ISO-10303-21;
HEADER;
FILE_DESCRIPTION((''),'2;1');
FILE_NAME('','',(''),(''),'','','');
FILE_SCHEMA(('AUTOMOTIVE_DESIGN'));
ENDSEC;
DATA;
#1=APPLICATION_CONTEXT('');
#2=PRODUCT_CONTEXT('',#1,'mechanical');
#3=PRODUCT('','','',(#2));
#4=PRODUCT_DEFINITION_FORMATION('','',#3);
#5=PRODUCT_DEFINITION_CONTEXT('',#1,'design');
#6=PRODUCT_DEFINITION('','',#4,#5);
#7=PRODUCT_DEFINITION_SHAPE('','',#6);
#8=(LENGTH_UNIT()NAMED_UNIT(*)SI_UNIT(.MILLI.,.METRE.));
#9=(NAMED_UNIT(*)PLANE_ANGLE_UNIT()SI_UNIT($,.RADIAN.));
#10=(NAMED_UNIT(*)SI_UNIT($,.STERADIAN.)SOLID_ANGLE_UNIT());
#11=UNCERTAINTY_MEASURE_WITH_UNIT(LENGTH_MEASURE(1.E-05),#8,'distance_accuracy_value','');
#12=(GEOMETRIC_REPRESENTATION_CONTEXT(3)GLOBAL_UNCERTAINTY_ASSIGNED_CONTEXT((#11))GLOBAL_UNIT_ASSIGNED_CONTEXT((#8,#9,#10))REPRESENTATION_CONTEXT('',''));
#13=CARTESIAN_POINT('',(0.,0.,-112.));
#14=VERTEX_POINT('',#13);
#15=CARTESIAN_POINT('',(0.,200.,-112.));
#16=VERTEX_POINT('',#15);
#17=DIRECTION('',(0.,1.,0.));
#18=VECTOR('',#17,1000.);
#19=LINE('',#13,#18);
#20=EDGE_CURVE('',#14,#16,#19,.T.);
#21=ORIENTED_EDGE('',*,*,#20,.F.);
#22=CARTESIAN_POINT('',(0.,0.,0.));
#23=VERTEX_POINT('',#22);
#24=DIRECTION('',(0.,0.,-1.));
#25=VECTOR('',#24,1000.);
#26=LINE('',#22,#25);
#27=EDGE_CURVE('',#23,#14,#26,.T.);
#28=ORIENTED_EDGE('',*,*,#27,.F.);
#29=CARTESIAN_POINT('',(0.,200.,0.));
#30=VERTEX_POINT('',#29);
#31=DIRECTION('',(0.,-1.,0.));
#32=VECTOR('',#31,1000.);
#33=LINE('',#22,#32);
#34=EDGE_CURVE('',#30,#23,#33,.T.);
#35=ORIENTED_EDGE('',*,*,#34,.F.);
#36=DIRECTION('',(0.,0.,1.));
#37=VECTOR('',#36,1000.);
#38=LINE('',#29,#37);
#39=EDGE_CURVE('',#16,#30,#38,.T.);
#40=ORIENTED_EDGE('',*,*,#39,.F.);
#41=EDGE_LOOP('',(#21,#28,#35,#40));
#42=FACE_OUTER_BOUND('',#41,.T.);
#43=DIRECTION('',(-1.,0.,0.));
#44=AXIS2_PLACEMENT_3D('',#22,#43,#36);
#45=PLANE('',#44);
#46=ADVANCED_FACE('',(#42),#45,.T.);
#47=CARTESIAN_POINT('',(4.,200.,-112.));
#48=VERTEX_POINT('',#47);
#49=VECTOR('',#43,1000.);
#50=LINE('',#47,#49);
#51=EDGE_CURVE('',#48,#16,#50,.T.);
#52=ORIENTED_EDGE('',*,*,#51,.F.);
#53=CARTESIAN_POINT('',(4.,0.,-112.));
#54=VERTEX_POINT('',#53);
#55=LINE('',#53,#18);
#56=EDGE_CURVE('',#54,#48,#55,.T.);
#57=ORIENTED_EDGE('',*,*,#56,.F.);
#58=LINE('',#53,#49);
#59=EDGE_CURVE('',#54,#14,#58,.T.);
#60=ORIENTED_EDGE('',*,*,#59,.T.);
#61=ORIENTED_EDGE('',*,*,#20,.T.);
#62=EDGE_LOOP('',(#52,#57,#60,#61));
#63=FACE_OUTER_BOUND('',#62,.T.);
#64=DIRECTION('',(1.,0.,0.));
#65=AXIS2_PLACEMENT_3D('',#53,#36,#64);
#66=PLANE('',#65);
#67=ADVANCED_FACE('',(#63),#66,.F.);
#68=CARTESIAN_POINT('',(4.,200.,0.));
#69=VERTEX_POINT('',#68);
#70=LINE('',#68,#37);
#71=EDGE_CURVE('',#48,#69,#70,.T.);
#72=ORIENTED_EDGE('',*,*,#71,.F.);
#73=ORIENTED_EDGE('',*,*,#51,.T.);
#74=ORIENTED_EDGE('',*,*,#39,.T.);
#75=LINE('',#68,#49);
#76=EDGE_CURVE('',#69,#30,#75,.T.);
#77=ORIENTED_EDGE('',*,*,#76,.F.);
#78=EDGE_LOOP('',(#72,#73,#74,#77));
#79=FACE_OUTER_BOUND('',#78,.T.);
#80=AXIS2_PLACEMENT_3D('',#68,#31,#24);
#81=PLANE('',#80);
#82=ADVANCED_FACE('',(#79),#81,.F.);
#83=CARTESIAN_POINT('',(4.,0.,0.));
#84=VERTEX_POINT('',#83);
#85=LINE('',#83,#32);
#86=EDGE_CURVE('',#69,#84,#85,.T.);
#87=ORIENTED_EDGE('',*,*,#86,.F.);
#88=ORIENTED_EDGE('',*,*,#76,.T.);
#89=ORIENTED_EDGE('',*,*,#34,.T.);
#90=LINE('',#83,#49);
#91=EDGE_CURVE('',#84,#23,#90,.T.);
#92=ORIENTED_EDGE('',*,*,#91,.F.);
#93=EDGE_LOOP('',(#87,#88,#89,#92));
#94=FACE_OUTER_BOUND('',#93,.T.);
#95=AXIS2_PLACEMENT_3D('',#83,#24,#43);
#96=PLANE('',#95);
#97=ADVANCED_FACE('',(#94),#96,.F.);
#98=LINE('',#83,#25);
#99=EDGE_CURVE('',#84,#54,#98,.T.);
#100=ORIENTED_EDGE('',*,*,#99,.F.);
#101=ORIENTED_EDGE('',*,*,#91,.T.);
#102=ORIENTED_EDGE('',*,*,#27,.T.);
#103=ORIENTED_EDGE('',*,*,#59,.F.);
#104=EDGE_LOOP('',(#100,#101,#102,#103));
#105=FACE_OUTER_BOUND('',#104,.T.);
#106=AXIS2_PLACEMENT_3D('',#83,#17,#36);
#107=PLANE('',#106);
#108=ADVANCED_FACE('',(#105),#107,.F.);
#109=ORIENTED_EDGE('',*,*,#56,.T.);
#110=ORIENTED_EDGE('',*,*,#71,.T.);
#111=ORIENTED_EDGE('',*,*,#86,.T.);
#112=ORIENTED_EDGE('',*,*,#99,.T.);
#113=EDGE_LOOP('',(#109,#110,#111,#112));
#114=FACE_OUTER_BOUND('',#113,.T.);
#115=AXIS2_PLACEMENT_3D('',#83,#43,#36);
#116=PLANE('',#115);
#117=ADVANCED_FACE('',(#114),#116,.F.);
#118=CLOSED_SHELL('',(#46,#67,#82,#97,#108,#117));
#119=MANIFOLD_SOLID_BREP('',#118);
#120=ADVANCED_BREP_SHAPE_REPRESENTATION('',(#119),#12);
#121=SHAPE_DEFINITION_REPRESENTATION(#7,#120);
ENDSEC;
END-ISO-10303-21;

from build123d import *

# Parameters (mm, degrees)
SKETCH_1_W      = 112
SKETCH_1_H      = 200
EXTRUDE_1_DEPTH = 4


with BuildPart() as part:
    # 草图1 → 凸台-拉伸1 (new body)
    with BuildSketch(Plane(origin=(0, 0, 0), x_dir=(0, 0, -1), z_dir=(1, 0, 0))):
        with Locations((56, 100)):
            Rectangle(SKETCH_1_W, SKETCH_1_H)
    extrude(amount=EXTRUDE_1_DEPTH)


solid = part.part
